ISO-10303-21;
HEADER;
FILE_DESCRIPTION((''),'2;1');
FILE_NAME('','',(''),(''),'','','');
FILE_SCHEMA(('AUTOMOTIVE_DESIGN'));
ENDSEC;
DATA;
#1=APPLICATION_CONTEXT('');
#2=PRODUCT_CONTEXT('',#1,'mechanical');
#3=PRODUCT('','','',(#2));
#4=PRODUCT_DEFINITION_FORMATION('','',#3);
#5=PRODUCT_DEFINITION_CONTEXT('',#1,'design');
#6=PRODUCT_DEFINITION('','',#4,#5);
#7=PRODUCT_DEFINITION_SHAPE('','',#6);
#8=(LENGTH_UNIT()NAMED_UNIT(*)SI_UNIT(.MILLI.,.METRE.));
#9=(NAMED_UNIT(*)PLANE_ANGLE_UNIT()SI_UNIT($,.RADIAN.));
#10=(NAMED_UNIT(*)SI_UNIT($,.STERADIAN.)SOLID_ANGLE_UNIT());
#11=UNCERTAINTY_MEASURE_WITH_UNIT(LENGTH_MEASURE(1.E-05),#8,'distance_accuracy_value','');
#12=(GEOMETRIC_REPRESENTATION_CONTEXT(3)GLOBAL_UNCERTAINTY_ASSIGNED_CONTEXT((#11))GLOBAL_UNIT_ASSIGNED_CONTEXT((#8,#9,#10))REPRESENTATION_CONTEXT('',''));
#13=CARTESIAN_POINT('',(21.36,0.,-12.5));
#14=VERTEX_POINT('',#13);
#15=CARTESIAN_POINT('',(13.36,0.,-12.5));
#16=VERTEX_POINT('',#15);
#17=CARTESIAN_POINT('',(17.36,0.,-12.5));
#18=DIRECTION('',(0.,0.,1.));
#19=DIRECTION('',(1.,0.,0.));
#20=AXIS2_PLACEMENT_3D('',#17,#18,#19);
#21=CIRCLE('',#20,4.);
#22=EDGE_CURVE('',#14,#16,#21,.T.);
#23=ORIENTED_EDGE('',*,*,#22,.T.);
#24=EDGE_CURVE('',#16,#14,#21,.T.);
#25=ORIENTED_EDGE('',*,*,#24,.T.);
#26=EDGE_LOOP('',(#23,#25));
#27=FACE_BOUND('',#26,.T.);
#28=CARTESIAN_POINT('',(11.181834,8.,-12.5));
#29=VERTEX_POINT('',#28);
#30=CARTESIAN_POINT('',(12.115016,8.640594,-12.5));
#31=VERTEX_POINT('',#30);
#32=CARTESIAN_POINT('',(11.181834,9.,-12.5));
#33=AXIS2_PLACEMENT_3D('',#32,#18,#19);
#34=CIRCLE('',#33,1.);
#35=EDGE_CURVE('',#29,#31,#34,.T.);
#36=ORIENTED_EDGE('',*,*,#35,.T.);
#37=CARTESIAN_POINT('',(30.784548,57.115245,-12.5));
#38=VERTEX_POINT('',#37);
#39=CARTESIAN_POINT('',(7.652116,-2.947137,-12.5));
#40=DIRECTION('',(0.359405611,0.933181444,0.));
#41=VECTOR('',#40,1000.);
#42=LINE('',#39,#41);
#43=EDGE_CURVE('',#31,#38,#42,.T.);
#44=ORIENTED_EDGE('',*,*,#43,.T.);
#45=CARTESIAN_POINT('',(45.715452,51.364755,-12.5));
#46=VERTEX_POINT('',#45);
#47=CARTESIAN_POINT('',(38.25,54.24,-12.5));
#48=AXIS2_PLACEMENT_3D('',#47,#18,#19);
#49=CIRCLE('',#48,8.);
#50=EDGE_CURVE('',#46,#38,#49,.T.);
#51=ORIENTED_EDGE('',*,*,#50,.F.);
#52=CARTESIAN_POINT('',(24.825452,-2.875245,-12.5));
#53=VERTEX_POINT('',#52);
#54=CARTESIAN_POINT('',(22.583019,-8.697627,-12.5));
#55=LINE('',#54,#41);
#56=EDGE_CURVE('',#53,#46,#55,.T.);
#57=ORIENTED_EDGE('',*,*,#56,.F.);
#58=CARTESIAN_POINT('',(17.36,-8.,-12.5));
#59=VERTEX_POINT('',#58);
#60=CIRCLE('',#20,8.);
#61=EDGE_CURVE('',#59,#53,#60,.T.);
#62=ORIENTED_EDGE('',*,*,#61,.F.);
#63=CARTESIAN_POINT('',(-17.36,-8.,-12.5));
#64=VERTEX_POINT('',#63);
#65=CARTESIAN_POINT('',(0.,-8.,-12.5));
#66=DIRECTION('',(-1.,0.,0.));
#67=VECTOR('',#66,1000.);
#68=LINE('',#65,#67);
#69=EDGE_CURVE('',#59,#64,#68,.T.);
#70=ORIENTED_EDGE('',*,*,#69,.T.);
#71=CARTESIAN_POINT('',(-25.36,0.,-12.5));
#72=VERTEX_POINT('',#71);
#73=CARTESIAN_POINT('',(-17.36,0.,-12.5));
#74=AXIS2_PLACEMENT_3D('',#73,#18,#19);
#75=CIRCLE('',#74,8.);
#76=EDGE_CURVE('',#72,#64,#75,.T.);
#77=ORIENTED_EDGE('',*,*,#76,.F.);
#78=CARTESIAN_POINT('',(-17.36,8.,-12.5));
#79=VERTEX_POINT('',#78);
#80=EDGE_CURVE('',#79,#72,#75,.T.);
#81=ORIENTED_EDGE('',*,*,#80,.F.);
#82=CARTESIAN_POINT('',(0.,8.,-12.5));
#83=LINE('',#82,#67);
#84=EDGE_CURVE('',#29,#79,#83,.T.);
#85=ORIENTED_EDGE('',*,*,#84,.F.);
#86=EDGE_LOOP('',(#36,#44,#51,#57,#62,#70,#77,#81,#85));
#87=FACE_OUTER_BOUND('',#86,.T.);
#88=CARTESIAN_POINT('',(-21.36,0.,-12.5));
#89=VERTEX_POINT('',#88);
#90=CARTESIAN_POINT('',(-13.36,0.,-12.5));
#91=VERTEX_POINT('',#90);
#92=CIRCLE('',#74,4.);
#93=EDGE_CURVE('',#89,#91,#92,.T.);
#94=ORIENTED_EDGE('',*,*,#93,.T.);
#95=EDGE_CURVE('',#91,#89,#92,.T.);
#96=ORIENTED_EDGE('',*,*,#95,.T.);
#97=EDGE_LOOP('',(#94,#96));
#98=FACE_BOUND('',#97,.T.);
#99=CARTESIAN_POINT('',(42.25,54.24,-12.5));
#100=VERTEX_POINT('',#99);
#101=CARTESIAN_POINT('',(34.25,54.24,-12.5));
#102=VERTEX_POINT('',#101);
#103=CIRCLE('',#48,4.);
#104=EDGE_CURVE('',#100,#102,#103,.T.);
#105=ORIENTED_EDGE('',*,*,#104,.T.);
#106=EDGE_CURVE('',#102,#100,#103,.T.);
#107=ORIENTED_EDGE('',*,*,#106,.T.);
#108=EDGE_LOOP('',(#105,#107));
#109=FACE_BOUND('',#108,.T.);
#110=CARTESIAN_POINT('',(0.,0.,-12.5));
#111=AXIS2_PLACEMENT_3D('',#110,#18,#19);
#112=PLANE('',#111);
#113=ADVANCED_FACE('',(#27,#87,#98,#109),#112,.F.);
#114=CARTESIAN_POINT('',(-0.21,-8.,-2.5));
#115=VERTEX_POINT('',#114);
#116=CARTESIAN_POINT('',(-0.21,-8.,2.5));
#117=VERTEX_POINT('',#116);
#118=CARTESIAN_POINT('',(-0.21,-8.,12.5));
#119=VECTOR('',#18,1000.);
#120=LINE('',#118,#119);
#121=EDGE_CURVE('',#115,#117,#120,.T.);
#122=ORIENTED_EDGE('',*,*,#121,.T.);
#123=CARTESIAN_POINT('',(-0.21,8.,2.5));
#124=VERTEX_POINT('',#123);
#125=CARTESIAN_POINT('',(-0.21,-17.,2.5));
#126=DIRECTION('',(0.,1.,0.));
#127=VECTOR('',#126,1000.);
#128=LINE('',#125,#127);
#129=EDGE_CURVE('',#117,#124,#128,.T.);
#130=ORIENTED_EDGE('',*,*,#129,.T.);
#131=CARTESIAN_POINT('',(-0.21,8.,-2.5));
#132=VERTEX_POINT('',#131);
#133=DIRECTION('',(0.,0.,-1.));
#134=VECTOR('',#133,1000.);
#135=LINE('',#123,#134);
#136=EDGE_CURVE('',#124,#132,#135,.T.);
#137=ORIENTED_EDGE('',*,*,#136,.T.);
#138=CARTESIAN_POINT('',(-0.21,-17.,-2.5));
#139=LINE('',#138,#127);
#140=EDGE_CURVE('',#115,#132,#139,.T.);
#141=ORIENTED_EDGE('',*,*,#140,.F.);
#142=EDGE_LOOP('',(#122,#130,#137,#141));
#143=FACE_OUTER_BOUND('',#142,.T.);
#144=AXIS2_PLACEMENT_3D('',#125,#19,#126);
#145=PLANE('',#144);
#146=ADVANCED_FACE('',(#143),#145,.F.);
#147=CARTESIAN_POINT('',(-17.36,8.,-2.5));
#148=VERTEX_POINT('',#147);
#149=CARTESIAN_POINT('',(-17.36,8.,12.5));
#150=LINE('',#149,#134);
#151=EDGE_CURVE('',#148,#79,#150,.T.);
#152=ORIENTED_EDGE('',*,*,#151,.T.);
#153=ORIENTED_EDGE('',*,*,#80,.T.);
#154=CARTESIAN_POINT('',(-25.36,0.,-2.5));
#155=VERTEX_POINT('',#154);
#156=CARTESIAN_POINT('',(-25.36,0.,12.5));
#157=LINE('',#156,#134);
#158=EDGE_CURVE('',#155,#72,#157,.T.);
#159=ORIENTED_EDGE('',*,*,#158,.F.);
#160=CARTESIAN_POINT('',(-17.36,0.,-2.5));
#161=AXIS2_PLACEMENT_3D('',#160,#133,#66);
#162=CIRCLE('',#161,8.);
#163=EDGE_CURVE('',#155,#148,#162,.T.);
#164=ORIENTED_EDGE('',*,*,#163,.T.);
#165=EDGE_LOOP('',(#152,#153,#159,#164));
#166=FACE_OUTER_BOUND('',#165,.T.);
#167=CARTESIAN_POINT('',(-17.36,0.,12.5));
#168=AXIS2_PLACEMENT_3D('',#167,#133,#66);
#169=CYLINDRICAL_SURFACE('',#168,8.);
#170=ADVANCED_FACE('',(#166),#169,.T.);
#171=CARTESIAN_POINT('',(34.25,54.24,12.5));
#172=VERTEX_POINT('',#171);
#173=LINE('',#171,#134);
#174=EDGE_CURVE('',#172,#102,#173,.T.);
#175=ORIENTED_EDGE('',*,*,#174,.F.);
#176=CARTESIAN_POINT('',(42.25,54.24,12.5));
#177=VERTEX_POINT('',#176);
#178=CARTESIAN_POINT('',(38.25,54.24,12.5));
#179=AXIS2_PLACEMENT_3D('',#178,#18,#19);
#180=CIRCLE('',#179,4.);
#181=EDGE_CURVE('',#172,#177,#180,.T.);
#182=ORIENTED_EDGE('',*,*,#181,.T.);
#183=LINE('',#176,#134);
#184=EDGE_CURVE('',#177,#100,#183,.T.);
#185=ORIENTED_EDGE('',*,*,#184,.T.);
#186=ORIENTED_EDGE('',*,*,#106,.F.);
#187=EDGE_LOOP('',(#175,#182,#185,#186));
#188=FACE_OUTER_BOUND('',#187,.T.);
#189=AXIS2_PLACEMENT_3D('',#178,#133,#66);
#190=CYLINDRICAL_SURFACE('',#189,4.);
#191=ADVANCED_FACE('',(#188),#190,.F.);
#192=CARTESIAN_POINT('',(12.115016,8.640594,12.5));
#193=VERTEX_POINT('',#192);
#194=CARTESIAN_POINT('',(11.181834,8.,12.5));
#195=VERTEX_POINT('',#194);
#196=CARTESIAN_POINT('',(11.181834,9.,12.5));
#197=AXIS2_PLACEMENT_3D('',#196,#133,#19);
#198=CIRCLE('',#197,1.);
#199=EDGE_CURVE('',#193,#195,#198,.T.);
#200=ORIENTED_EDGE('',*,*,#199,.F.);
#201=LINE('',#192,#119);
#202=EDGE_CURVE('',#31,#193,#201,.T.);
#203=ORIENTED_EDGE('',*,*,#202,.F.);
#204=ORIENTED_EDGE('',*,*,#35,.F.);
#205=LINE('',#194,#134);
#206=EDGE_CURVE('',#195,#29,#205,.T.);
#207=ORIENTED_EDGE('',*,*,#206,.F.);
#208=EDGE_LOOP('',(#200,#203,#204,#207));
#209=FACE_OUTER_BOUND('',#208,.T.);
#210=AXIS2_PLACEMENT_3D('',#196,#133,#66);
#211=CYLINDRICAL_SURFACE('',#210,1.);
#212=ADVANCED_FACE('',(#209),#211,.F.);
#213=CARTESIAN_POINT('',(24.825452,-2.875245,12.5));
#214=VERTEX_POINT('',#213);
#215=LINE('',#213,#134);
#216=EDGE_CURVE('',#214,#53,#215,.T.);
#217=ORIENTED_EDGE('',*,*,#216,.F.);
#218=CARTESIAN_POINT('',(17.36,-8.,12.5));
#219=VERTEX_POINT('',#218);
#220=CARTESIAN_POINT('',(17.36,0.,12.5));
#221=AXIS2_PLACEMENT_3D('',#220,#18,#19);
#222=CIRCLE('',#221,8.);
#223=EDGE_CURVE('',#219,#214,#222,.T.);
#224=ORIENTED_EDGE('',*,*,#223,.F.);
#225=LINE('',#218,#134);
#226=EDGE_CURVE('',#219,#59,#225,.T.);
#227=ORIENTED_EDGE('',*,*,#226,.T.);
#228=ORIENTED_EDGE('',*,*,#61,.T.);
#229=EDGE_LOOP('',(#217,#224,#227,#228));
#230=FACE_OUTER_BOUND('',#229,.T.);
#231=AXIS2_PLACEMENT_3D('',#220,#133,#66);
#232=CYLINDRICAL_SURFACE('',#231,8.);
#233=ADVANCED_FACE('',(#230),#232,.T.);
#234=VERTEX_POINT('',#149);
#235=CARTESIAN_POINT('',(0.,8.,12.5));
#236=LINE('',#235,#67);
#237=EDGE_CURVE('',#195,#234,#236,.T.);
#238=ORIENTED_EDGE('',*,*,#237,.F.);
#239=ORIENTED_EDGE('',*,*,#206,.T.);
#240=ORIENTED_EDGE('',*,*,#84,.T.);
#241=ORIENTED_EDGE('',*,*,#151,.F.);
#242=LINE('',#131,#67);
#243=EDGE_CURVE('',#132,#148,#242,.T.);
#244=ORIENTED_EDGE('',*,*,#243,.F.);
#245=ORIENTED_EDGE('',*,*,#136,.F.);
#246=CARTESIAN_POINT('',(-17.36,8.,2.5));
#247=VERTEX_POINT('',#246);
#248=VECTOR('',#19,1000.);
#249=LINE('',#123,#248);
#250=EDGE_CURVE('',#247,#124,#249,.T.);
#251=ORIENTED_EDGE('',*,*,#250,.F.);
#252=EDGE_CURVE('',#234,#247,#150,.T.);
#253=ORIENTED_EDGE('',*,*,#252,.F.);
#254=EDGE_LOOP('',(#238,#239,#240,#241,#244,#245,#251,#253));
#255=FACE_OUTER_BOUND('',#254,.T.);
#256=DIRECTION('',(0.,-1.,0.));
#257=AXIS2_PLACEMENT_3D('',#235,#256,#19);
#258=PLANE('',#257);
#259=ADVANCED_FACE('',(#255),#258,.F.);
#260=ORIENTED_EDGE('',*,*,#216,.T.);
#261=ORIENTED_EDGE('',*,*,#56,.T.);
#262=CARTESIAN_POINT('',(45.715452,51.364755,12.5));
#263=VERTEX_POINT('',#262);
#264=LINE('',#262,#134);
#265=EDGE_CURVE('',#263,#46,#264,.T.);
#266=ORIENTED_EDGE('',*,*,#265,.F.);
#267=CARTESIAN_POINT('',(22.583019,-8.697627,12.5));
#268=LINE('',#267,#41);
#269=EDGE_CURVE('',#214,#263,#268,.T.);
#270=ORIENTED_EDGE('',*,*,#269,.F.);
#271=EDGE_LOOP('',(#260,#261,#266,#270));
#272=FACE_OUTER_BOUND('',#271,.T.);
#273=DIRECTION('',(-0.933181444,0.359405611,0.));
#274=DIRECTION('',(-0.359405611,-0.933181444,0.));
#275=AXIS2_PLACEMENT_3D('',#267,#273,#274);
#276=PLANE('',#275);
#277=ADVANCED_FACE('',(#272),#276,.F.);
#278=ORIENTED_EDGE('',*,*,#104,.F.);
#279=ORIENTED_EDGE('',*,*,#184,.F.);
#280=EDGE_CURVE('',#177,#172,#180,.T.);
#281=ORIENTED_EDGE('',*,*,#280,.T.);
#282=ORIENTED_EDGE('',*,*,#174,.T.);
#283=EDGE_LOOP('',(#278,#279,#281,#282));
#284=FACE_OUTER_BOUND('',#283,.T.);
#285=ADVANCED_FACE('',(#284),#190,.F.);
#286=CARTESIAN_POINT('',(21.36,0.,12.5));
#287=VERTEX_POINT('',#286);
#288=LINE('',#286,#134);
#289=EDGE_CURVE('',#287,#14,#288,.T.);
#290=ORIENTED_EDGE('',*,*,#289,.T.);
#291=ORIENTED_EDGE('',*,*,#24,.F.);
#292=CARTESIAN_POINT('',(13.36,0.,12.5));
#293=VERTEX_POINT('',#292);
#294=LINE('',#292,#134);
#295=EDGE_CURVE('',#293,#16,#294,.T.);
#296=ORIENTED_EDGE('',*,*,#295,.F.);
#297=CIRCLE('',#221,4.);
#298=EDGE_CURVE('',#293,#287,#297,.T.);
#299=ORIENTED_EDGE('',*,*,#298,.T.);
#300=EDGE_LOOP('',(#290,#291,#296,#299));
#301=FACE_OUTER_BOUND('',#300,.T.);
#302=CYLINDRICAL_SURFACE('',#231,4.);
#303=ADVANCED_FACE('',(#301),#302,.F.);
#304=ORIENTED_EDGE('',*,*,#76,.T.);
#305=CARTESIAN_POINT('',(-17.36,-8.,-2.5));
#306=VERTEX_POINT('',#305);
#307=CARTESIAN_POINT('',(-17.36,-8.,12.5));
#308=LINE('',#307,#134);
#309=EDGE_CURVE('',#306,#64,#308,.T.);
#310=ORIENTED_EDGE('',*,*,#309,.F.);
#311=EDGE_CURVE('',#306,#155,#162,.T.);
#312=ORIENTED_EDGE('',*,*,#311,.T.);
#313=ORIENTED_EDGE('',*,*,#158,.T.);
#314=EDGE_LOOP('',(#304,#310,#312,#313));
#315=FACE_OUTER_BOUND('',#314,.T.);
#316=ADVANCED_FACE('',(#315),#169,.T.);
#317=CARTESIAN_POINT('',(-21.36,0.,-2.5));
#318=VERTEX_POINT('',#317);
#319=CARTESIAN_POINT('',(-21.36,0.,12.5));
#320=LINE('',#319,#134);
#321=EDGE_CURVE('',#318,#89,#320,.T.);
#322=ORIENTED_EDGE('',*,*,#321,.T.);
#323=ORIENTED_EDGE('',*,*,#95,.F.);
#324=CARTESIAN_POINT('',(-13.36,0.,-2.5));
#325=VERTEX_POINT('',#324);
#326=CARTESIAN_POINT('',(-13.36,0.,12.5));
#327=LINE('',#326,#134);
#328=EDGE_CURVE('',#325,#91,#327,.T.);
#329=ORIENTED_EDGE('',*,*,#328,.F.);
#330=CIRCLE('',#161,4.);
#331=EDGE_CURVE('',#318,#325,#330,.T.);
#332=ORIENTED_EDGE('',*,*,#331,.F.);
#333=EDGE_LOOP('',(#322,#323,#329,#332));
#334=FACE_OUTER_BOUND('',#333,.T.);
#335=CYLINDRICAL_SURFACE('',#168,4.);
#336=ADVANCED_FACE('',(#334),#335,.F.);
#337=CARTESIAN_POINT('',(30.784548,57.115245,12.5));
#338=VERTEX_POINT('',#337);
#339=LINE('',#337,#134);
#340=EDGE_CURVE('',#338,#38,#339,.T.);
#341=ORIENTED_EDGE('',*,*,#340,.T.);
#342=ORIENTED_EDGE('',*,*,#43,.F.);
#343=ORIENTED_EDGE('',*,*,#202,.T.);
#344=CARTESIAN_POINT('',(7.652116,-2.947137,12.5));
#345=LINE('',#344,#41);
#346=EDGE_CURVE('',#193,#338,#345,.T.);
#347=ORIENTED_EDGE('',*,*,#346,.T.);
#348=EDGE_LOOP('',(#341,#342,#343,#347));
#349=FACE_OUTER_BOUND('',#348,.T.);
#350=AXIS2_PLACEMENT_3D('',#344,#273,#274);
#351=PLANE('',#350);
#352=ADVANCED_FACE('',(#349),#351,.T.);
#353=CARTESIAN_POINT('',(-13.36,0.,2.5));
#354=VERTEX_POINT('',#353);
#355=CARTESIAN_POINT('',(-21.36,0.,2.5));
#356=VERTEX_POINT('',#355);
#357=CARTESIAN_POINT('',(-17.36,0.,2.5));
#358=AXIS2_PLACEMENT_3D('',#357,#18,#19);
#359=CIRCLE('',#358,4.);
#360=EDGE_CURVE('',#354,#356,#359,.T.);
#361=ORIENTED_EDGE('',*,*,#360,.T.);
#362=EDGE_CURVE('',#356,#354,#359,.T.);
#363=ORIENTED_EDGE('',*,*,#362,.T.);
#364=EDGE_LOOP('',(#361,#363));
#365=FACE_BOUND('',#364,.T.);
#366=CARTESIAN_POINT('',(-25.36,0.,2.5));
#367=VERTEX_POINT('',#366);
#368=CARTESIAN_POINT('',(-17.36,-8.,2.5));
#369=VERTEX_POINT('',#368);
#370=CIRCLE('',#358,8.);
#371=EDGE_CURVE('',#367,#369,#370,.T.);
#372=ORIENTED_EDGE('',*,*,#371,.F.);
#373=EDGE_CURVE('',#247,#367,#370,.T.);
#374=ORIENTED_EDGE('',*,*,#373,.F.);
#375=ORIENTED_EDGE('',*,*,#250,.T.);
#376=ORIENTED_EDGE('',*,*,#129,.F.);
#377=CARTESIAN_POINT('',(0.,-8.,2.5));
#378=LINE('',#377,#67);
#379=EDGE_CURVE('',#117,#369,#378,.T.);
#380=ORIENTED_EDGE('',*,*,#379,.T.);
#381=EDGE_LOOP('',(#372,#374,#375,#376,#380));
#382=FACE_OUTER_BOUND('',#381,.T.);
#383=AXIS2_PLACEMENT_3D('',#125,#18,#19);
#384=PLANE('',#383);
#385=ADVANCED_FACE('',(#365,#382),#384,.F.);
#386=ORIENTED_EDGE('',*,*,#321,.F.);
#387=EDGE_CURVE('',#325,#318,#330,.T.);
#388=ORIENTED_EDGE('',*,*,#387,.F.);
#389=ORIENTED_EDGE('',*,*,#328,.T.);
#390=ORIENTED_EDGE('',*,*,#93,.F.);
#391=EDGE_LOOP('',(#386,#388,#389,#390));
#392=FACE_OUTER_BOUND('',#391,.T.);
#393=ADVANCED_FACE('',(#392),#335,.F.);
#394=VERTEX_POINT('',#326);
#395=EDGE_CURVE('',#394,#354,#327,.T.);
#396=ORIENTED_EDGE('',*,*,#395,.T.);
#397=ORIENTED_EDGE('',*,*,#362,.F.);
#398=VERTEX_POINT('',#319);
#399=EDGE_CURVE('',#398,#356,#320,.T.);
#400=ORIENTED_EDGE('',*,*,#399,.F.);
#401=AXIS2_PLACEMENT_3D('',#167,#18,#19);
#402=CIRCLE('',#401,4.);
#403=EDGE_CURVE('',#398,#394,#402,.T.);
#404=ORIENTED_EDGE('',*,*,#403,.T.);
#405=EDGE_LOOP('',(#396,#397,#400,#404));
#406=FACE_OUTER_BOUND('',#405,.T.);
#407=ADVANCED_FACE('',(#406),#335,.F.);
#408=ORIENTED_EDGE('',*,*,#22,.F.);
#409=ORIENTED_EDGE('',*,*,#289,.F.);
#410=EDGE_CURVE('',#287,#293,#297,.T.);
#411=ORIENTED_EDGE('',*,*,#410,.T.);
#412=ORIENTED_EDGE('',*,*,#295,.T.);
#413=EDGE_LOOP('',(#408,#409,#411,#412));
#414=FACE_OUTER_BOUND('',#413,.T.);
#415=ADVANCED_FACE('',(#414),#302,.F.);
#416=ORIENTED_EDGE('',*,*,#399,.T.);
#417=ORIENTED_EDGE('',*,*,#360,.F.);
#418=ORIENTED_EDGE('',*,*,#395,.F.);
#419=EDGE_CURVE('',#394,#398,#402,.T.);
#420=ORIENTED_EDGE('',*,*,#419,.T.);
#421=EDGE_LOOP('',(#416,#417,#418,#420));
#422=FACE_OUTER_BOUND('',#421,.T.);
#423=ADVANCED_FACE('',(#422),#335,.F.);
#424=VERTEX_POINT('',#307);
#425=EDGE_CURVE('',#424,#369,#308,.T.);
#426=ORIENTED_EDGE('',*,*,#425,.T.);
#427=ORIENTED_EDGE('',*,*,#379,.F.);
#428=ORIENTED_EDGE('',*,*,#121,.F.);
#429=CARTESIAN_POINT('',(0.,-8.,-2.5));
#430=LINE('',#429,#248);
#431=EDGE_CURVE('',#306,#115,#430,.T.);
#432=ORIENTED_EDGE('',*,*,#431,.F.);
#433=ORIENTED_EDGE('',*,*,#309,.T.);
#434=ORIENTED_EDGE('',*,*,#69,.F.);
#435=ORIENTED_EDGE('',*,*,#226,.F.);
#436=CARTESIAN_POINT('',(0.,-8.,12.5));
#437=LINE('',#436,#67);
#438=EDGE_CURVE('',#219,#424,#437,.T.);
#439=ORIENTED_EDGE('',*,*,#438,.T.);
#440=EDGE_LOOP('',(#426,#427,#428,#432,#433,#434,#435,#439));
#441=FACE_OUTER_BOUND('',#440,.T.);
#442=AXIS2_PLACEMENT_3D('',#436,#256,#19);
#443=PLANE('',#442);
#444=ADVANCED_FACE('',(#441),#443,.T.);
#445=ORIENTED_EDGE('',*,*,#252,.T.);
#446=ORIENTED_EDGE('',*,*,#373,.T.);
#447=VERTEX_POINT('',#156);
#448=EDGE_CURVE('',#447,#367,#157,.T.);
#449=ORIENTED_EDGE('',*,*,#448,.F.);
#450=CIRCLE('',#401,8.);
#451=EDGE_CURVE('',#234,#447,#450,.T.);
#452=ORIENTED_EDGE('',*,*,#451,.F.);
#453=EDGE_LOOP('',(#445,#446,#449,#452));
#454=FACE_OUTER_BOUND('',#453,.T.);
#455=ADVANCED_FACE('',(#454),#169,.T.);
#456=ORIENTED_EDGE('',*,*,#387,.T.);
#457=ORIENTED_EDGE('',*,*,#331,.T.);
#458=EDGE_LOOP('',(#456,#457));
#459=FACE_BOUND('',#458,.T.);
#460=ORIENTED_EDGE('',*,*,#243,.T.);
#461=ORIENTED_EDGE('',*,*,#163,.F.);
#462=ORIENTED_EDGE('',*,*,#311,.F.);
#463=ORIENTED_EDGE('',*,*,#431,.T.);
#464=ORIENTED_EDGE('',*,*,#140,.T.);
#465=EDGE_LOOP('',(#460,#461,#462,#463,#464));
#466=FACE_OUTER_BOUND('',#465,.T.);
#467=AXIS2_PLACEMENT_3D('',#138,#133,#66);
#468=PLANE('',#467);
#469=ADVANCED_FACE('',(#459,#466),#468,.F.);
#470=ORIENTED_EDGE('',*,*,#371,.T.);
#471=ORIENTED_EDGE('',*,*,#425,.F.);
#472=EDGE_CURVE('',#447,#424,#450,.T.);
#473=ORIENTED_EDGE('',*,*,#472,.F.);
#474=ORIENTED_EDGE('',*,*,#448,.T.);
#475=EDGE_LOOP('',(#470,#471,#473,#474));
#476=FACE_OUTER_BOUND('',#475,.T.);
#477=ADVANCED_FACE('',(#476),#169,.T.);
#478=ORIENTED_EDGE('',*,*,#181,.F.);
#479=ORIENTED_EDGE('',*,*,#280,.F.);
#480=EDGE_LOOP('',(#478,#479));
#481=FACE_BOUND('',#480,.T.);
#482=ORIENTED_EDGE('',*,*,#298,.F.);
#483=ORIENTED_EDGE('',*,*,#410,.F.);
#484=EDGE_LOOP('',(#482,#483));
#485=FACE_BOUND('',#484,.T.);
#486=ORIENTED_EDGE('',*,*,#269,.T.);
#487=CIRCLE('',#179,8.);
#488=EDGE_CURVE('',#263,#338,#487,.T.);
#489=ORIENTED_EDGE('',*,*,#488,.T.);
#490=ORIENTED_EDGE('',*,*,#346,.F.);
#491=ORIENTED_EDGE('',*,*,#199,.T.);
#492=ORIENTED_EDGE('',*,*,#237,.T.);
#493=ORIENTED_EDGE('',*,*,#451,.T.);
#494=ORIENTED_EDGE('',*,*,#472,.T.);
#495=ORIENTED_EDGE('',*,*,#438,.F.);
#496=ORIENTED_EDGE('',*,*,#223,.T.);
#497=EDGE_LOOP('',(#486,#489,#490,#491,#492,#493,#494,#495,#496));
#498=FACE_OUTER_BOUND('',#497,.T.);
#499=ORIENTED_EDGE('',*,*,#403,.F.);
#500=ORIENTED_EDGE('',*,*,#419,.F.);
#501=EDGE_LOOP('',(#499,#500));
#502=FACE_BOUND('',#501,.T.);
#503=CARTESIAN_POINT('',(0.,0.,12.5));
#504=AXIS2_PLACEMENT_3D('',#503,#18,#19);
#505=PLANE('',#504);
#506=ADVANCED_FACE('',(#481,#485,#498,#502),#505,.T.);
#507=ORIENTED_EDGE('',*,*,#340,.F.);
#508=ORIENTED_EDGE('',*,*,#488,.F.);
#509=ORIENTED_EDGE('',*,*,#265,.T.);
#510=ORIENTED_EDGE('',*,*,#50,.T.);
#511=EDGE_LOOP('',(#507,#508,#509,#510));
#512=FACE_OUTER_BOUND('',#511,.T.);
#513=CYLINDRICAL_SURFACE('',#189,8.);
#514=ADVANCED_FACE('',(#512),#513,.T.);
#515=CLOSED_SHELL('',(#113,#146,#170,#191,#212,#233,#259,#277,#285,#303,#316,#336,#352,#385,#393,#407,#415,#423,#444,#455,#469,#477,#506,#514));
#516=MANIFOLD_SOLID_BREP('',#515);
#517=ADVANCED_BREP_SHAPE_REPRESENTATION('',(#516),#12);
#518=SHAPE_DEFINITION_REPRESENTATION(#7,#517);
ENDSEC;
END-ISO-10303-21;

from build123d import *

# Parameters (mm, degrees)
JAW_PROFILE_SKETCH_R = 4
JAW_BODY_25MM_DEPTH  = 12.5
SLOT_SKETCH_W        = 25.15
SLOT_SKETCH_H        = 5
SLOT_CUT_5MM_DEPTH   = 25
EDGE_FILLETS_R1_R    = 1


with BuildPart() as part:
    # Jaw Profile Sketch → Jaw Body 25mm (new, symmetric)
    with BuildSketch(Plane.XY):
        with BuildLine():
            Line((24.825451548, -2.87524489), (45.715451548, 51.36475511))
            ThreePointArc((45.715451548, 51.36475511), (41.12524489, 61.705451548), (30.784548452, 57.11524489))
            Line((30.784548452, 57.11524489), (11.868297239, 8))
            Line((11.868297239, 8), (-17.36, 8))
            ThreePointArc((-17.36, 8), (-25.36, 0), (-17.36, -8))
            Line((-17.36, -8), (17.36, -8))
            ThreePointArc((17.36, -8), (21.887584393, -6.595527239), (24.825451548, -2.87524489))
        make_face()
        with Locations((38.25, 54.24)):
            Circle(JAW_PROFILE_SKETCH_R, mode=Mode.SUBTRACT)
        with Locations((-17.36, 0)):
            Circle(JAW_PROFILE_SKETCH_R, mode=Mode.SUBTRACT)
        with Locations((17.36, 0)):
            Circle(JAW_PROFILE_SKETCH_R, mode=Mode.SUBTRACT)
    extrude(amount=JAW_BODY_25MM_DEPTH, both=True)

    # Slot Sketch → Slot Cut 5mm (cut)
    with BuildSketch(Plane(origin=(0, 8, 0), x_dir=(1, 0, 0), z_dir=(0, 1, 0))):
        with Locations((-12.785, 0)):
            Rectangle(SLOT_SKETCH_W, SLOT_SKETCH_H)
    extrude(amount=-SLOT_CUT_5MM_DEPTH, mode=Mode.SUBTRACT)

    # Edge Fillets R1
    edge_fillets_r1_edges = [part.edges().sort_by_distance(p)[0] for p in [
        (11.868297239, 8, 0),
    ]]
    fillet(edge_fillets_r1_edges, radius=EDGE_FILLETS_R1_R)


solid = part.part
